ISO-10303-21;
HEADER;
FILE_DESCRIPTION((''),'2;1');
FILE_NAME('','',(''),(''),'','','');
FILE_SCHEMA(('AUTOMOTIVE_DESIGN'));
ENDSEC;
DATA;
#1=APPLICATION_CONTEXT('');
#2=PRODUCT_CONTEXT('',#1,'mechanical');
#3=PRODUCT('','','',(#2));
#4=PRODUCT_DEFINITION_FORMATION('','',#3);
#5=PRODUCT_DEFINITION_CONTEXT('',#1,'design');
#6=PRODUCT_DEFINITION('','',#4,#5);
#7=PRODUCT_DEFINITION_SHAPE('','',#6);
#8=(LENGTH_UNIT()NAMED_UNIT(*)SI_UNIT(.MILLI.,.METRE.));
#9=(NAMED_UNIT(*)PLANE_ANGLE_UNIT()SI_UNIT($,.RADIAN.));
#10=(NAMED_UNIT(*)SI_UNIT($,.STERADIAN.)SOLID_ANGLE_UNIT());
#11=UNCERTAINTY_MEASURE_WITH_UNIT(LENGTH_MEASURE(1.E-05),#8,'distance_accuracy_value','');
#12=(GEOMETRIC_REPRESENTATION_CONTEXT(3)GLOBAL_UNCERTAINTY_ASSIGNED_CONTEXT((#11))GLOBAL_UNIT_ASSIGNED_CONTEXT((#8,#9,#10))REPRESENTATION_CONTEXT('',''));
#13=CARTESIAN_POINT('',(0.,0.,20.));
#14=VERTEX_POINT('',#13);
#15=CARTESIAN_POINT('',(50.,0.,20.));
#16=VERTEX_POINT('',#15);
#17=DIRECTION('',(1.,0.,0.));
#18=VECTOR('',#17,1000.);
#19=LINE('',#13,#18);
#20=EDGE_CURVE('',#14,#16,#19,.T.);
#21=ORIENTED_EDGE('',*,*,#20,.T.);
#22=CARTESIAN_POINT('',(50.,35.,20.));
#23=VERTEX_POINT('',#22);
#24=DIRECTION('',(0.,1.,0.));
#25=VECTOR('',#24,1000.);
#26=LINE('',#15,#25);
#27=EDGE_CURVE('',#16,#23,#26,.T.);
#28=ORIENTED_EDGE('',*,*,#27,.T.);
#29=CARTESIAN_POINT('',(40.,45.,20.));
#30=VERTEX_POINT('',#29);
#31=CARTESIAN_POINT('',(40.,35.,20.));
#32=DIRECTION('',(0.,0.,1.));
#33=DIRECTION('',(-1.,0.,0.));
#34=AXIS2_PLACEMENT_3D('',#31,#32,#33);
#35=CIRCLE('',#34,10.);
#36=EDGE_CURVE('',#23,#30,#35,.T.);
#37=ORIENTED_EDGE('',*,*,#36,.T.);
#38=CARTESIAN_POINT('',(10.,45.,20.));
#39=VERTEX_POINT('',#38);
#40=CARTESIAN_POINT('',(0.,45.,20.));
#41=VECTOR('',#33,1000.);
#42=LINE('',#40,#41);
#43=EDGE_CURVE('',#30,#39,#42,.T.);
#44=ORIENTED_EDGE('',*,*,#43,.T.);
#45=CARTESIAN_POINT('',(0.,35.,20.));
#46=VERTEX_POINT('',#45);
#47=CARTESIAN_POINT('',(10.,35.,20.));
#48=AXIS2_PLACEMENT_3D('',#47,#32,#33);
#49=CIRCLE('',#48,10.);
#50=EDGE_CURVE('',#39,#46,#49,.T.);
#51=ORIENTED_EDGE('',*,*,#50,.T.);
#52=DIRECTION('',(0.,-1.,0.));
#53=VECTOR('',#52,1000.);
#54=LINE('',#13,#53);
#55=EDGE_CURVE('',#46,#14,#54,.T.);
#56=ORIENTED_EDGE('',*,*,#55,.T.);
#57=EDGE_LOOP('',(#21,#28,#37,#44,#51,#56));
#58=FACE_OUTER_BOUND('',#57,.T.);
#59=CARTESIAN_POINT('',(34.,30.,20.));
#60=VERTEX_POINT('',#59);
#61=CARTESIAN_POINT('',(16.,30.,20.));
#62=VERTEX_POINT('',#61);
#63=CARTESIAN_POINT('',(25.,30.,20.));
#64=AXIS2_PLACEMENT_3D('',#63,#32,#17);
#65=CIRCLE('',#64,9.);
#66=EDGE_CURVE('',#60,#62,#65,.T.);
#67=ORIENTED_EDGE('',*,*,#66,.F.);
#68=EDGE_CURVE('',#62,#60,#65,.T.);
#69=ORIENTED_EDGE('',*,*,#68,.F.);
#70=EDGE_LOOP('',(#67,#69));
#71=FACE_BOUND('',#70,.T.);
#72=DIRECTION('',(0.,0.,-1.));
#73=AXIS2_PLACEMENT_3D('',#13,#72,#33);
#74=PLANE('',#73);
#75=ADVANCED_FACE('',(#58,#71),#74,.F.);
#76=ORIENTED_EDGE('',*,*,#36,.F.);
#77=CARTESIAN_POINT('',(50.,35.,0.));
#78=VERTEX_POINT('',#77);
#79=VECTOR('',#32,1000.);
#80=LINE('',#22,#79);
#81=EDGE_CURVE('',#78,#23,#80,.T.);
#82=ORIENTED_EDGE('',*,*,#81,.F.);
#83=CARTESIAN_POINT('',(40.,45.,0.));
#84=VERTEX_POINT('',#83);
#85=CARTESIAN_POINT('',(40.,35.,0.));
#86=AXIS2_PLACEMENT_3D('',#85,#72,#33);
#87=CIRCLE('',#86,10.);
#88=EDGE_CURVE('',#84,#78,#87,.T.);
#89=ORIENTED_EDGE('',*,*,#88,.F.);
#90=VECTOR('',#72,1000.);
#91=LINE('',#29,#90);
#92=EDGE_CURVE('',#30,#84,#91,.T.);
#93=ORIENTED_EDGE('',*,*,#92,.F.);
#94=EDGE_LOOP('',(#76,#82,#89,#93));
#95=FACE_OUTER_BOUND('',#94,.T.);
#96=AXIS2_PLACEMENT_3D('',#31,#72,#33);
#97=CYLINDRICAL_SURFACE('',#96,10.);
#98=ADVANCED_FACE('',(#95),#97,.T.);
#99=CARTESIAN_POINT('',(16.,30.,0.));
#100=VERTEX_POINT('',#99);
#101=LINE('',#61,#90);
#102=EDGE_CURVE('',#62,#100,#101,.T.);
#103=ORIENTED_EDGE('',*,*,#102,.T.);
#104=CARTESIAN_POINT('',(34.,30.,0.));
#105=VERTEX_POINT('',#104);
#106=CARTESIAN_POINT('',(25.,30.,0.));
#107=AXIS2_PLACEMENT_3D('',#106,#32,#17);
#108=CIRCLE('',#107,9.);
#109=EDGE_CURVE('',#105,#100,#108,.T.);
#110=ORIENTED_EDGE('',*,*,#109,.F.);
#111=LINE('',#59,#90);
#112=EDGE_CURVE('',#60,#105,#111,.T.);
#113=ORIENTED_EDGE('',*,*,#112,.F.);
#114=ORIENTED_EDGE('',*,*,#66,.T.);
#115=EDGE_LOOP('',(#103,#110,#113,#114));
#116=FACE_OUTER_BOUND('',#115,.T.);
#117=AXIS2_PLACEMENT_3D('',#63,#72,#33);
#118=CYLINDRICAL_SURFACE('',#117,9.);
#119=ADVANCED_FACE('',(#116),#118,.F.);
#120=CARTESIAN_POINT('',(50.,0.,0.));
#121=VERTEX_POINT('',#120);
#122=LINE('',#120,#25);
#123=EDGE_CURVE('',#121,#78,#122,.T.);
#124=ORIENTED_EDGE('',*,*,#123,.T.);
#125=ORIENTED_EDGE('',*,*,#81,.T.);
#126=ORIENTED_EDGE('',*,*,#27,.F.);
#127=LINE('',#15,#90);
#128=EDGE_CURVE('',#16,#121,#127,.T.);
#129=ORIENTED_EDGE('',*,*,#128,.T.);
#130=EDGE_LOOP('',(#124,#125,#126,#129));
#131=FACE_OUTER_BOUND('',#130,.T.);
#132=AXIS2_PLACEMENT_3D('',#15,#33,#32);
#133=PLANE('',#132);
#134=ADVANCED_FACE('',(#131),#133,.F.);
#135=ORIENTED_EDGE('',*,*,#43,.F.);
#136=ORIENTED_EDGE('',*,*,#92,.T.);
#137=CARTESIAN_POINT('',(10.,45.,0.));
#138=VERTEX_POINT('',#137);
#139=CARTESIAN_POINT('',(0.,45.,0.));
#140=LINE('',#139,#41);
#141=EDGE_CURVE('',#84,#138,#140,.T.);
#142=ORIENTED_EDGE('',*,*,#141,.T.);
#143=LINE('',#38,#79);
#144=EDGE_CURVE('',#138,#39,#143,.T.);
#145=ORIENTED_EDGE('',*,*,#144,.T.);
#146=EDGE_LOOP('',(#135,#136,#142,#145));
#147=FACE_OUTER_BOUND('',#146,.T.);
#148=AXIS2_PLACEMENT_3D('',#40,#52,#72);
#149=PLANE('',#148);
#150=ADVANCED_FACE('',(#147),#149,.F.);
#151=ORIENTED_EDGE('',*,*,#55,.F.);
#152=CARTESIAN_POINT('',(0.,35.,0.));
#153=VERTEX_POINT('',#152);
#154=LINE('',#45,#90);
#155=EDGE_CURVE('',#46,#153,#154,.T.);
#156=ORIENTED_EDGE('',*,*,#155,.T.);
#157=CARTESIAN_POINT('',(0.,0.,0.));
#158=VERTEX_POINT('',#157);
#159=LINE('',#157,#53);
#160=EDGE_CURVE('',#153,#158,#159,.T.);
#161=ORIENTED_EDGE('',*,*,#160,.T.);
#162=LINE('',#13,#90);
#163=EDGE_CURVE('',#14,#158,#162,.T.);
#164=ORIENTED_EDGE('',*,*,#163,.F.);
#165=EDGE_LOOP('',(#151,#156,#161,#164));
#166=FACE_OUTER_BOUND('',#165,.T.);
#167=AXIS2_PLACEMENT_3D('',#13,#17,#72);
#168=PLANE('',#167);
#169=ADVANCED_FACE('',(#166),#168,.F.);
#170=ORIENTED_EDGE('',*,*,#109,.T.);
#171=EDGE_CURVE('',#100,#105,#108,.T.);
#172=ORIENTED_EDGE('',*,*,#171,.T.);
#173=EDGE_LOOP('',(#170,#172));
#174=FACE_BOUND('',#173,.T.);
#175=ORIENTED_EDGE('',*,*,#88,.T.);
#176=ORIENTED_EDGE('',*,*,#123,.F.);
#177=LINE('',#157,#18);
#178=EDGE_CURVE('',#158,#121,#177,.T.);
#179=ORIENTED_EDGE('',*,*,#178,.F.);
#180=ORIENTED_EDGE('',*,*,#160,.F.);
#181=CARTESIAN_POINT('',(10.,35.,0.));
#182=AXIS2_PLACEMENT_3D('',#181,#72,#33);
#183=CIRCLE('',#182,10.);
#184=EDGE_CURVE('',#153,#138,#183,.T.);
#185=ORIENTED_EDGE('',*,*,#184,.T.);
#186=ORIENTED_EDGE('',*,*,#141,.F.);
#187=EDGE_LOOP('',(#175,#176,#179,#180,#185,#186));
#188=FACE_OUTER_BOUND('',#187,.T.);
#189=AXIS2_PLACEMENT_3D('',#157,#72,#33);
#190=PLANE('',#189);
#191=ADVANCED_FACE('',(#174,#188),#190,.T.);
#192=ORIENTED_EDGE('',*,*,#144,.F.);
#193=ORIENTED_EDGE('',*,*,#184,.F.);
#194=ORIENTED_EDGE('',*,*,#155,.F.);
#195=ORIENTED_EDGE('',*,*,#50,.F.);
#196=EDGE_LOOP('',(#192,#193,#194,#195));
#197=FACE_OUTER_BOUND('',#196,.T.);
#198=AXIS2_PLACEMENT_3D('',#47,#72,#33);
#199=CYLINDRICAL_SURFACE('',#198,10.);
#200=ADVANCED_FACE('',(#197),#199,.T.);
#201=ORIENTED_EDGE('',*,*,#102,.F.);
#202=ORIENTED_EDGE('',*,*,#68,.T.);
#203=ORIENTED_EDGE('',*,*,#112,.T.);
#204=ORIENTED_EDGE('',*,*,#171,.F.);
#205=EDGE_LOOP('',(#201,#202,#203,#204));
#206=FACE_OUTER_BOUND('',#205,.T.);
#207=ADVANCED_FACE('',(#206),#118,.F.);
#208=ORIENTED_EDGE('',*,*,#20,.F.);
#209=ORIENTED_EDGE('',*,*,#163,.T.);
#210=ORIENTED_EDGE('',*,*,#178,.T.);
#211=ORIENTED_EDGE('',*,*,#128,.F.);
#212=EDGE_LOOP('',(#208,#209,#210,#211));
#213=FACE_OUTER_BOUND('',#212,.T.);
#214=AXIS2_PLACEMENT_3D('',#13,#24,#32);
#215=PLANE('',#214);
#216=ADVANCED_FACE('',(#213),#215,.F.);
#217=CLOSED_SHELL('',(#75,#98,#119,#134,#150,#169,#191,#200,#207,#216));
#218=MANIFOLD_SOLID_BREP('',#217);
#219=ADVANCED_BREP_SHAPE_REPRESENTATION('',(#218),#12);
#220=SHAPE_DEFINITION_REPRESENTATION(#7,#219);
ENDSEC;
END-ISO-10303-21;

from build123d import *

# Parameters (mm, degrees)
SKETCH1_W           = 50
SKETCH1_H           = 45
SKETCH1_R           = 9
BOSS_EXTRUDE1_DEPTH = 20
FILLET1_R           = 10


with BuildPart() as part:
    # Sketch1 → Boss-Extrude1 (new body)
    with BuildSketch(Plane.XY):
        with Locations((25, 22.5)):
            Rectangle(SKETCH1_W, SKETCH1_H)
        with Locations((25, 30)):
            Circle(SKETCH1_R, mode=Mode.SUBTRACT)
    extrude(amount=BOSS_EXTRUDE1_DEPTH)

    # Fillet1
    fillet1_edges = [part.edges().sort_by_distance(p)[0] for p in [
        (0, 45, 10),
        (50, 45, 10),
    ]]
    fillet(fillet1_edges, radius=FILLET1_R)


solid = part.part
